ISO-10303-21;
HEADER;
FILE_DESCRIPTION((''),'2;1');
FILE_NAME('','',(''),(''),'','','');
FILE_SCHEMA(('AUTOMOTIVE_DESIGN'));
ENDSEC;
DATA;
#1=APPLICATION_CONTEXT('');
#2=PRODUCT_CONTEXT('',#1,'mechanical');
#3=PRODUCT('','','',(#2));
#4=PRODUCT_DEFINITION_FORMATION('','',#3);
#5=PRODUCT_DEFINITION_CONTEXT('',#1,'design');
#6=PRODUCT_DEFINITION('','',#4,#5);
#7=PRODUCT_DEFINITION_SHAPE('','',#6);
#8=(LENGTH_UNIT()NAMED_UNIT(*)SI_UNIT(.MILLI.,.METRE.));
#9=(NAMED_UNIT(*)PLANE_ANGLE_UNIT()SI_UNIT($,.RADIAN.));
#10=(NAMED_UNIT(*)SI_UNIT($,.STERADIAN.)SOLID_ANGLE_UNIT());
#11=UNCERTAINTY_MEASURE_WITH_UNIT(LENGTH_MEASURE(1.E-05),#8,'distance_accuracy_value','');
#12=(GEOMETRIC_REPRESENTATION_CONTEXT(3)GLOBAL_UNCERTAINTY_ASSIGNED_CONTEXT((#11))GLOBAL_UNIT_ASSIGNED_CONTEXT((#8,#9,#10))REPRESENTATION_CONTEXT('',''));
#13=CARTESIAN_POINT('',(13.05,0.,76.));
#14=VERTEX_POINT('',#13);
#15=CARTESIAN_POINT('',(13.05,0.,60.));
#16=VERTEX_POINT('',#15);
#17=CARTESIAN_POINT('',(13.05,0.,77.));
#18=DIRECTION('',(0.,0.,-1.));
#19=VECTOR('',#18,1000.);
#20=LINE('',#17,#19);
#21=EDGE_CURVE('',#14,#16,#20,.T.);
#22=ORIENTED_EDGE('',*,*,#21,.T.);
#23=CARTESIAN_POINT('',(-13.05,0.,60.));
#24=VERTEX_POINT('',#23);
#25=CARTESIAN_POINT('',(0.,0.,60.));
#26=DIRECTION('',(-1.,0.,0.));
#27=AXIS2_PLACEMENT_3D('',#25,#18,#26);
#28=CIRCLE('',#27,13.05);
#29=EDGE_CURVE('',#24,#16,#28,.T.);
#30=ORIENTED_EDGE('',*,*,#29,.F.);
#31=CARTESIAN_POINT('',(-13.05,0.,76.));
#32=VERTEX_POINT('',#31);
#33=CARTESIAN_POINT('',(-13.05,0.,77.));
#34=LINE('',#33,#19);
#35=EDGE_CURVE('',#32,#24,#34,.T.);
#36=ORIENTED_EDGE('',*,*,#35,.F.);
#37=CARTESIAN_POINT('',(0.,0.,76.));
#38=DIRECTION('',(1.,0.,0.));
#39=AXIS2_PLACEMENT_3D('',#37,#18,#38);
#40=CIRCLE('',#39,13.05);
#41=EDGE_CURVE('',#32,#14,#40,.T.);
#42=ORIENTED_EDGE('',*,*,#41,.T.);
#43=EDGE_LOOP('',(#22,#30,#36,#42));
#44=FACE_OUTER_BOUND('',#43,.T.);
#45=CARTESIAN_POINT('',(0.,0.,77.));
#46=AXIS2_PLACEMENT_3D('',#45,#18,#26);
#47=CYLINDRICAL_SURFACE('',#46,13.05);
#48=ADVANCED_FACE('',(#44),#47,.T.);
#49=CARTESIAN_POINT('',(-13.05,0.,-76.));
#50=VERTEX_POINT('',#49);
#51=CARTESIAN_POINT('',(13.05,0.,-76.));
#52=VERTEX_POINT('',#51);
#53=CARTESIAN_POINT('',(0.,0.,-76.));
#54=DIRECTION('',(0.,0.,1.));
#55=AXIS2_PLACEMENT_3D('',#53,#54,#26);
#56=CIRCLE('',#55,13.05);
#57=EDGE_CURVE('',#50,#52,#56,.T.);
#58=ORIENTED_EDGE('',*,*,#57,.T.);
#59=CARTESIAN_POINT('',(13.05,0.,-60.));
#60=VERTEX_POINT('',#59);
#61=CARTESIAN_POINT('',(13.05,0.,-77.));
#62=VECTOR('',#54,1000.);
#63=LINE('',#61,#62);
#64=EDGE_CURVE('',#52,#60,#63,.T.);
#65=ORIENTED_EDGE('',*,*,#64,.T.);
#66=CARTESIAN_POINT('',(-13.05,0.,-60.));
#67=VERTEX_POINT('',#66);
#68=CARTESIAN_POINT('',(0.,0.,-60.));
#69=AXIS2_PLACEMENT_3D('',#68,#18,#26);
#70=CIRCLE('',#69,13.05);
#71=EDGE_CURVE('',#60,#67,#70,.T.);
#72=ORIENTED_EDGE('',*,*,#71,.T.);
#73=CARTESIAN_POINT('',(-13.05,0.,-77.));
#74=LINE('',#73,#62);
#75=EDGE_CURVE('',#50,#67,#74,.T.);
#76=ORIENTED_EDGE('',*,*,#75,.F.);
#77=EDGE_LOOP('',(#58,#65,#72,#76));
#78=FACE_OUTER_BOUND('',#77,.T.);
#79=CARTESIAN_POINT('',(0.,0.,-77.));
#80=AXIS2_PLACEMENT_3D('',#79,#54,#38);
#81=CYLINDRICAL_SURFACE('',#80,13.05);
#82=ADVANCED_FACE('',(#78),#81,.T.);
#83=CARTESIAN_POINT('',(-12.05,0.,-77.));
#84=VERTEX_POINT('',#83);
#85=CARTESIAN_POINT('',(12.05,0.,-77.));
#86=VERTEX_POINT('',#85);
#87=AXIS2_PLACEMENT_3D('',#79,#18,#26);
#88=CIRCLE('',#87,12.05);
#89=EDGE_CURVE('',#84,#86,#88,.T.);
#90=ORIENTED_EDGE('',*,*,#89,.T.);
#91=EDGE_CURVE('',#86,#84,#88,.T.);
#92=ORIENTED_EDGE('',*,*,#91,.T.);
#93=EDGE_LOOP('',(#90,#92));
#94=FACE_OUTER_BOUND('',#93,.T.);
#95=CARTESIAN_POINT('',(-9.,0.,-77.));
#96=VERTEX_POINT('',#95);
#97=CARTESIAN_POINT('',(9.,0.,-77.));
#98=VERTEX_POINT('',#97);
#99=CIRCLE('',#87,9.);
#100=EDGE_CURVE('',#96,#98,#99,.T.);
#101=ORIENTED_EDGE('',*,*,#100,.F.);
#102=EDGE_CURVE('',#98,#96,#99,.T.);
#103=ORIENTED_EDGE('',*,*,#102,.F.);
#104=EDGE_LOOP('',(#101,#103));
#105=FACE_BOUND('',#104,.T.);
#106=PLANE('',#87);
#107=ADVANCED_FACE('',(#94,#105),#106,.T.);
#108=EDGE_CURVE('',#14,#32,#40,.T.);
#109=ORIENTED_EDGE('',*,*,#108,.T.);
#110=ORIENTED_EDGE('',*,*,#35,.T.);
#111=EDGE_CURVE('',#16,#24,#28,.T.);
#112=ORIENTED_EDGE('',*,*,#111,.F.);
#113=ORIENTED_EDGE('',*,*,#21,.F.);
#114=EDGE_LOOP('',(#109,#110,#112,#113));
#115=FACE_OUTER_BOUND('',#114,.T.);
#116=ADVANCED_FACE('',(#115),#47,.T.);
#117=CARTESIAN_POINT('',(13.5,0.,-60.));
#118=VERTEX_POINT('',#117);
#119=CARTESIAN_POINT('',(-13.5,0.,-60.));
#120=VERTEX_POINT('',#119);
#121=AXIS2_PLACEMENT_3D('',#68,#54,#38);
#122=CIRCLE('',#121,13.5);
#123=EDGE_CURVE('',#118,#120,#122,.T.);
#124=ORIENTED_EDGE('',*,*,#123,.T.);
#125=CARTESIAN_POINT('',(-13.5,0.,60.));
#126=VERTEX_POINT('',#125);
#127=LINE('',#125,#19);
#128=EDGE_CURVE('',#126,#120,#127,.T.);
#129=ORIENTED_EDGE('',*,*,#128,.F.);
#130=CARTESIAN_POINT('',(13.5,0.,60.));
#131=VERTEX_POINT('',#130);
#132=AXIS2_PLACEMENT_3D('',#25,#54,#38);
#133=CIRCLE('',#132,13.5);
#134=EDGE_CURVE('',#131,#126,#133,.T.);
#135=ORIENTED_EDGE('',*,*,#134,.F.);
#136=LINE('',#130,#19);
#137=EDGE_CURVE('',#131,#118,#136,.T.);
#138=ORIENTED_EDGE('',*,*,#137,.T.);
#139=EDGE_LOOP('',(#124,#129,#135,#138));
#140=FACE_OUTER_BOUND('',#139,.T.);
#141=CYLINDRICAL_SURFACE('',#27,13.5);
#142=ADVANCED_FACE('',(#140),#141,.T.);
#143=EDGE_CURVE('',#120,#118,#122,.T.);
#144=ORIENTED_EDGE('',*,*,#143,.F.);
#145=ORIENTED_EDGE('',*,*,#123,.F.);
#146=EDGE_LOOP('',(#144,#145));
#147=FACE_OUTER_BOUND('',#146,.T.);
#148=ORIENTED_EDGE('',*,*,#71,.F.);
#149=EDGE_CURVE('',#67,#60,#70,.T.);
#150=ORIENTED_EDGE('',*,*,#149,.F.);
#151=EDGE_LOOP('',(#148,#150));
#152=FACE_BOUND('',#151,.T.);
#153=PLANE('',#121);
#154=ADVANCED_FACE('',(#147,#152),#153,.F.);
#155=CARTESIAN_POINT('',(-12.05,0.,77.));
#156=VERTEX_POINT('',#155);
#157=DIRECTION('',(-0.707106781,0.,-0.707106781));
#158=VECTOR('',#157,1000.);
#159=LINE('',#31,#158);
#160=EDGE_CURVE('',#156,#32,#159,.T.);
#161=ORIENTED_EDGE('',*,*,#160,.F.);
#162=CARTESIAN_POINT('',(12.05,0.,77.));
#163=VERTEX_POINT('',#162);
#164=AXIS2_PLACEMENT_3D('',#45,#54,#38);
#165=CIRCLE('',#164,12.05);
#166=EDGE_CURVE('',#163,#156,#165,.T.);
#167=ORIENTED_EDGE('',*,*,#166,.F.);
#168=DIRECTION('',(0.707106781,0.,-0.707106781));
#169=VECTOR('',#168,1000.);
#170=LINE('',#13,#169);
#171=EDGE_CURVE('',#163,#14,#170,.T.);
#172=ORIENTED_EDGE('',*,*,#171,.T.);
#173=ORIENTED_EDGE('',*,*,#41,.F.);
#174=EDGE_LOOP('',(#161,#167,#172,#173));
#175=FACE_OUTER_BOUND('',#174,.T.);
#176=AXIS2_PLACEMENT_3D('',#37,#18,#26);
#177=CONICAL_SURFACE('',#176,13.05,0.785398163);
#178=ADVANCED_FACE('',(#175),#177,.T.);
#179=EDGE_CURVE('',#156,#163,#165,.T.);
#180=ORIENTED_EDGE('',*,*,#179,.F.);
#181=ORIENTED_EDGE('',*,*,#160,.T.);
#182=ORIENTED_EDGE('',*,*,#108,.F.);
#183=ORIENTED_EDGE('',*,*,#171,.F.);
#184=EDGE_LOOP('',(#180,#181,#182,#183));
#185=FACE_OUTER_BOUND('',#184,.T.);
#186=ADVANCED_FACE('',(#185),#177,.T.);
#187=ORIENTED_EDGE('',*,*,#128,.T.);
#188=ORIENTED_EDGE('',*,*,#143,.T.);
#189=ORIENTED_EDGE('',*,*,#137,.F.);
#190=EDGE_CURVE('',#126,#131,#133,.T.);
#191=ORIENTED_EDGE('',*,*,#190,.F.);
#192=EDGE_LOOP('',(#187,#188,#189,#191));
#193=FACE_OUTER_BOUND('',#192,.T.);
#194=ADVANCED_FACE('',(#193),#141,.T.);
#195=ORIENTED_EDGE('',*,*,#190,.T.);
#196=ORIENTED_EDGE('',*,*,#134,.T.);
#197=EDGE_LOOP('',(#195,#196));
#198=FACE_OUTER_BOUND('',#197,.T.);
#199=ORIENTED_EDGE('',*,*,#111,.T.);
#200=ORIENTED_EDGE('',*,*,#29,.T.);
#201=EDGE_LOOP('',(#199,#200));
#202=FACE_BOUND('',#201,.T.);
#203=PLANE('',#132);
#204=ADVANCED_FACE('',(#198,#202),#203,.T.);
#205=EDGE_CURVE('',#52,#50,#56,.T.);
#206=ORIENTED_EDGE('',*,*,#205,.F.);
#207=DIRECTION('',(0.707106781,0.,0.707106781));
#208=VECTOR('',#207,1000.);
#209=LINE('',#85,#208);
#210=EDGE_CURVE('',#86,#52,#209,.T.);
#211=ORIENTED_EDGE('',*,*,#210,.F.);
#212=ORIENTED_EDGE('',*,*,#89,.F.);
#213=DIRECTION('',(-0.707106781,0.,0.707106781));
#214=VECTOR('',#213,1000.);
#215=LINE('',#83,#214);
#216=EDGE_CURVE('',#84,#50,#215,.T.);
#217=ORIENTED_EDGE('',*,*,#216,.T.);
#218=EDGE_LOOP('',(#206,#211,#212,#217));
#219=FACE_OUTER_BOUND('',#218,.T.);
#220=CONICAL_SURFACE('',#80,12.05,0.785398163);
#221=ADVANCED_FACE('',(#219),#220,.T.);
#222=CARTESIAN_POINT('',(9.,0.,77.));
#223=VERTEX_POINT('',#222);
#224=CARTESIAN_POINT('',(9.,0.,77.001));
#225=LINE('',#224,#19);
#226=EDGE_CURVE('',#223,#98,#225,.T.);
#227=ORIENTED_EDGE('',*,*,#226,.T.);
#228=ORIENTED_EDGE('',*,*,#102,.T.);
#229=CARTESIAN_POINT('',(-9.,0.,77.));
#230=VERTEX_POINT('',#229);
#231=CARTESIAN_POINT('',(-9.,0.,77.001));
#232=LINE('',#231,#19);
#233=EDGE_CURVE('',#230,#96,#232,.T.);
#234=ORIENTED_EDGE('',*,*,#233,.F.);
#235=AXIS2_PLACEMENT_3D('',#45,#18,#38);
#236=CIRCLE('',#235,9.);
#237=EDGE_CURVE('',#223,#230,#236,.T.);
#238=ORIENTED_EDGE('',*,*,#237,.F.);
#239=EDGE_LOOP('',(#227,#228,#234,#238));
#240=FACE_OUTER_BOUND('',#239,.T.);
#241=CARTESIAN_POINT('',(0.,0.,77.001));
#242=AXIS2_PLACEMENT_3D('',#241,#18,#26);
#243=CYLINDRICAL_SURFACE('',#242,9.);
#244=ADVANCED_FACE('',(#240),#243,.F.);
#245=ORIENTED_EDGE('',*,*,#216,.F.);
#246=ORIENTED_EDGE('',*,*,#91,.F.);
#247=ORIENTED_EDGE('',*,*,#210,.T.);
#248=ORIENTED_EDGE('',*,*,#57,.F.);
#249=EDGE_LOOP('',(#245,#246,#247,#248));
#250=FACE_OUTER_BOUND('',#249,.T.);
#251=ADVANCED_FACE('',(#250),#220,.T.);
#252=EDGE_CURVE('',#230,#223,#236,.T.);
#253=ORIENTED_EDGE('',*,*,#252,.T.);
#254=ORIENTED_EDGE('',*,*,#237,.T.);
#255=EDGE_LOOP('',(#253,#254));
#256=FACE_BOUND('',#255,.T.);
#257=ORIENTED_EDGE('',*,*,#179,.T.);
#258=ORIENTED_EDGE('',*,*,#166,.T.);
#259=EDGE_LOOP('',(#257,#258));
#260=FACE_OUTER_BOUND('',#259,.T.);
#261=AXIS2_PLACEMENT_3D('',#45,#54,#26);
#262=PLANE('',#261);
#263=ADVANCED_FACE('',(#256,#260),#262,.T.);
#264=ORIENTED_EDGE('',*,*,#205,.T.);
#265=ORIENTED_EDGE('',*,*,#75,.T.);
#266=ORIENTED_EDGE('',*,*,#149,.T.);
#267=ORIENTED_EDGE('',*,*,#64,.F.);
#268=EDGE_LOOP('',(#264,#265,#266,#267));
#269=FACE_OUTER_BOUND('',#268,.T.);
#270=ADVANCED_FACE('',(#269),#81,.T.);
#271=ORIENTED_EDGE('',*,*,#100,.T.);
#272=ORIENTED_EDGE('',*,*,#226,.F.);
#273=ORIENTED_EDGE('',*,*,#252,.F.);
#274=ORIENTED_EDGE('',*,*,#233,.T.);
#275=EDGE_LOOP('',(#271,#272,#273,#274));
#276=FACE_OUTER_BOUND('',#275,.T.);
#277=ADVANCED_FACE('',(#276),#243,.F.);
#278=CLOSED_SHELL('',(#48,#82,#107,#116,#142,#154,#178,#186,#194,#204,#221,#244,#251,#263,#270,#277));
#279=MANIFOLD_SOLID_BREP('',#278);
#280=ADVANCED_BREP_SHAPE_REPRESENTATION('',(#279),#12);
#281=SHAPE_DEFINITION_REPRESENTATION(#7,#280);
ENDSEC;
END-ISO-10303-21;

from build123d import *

# Parameters (mm, degrees)
SKETCH_1_R          = 13.5
EXTRUDE_1_DEPTH     = 60
SKETCH_4_R          = 13.05
EXTRUDE_3_DEPTH     = 17
CUT_EXTRUDE_2_REACH = 157.179
SKETCH_5_R          = 9
CHAMFER_1_SIZE      = 1


with BuildPart() as part:
    # 草图1 → 凸台-拉伸1 (new, symmetric)
    with BuildSketch(Plane.XY):
        Circle(SKETCH_1_R)
    extrude(amount=EXTRUDE_1_DEPTH, both=True)

    # 草图4 → 凸台-拉伸3 (add)
    with BuildSketch(Plane(origin=(0, 0, -60), x_dir=(-1, 0, 0), z_dir=(0, 0, -1))):
        Circle(SKETCH_4_R)
    extrude_3 = extrude(amount=EXTRUDE_3_DEPTH)

    # 镜向1: 凸台-拉伸3 across plane
    add(extrude_3.mirror(Plane.XY))

    # 草图5 → 切除-拉伸2 (cut, up to next)
    with BuildSketch(Plane(origin=(0, 0, -77), x_dir=(-1, 0, 0), z_dir=(0, 0, -1)), mode=Mode.PRIVATE) as cut_extrude_2_sk1:
        Circle(SKETCH_5_R)
    cut_extrude_2_tool1 = extrude(cut_extrude_2_sk1.sketch, amount=-CUT_EXTRUDE_2_REACH, mode=Mode.PRIVATE) & part.part
    add(cut_extrude_2_tool1.solids().sort_by_distance((0, 0, -77))[0], mode=Mode.SUBTRACT)

    # 倒角1
    chamfer_1_edges = [part.edges().sort_by_distance(p)[0] for p in [
        (13.05, 0, 77),
        (13.05, 0, -77),
    ]]
    chamfer(chamfer_1_edges, length=CHAMFER_1_SIZE)


solid = part.part
